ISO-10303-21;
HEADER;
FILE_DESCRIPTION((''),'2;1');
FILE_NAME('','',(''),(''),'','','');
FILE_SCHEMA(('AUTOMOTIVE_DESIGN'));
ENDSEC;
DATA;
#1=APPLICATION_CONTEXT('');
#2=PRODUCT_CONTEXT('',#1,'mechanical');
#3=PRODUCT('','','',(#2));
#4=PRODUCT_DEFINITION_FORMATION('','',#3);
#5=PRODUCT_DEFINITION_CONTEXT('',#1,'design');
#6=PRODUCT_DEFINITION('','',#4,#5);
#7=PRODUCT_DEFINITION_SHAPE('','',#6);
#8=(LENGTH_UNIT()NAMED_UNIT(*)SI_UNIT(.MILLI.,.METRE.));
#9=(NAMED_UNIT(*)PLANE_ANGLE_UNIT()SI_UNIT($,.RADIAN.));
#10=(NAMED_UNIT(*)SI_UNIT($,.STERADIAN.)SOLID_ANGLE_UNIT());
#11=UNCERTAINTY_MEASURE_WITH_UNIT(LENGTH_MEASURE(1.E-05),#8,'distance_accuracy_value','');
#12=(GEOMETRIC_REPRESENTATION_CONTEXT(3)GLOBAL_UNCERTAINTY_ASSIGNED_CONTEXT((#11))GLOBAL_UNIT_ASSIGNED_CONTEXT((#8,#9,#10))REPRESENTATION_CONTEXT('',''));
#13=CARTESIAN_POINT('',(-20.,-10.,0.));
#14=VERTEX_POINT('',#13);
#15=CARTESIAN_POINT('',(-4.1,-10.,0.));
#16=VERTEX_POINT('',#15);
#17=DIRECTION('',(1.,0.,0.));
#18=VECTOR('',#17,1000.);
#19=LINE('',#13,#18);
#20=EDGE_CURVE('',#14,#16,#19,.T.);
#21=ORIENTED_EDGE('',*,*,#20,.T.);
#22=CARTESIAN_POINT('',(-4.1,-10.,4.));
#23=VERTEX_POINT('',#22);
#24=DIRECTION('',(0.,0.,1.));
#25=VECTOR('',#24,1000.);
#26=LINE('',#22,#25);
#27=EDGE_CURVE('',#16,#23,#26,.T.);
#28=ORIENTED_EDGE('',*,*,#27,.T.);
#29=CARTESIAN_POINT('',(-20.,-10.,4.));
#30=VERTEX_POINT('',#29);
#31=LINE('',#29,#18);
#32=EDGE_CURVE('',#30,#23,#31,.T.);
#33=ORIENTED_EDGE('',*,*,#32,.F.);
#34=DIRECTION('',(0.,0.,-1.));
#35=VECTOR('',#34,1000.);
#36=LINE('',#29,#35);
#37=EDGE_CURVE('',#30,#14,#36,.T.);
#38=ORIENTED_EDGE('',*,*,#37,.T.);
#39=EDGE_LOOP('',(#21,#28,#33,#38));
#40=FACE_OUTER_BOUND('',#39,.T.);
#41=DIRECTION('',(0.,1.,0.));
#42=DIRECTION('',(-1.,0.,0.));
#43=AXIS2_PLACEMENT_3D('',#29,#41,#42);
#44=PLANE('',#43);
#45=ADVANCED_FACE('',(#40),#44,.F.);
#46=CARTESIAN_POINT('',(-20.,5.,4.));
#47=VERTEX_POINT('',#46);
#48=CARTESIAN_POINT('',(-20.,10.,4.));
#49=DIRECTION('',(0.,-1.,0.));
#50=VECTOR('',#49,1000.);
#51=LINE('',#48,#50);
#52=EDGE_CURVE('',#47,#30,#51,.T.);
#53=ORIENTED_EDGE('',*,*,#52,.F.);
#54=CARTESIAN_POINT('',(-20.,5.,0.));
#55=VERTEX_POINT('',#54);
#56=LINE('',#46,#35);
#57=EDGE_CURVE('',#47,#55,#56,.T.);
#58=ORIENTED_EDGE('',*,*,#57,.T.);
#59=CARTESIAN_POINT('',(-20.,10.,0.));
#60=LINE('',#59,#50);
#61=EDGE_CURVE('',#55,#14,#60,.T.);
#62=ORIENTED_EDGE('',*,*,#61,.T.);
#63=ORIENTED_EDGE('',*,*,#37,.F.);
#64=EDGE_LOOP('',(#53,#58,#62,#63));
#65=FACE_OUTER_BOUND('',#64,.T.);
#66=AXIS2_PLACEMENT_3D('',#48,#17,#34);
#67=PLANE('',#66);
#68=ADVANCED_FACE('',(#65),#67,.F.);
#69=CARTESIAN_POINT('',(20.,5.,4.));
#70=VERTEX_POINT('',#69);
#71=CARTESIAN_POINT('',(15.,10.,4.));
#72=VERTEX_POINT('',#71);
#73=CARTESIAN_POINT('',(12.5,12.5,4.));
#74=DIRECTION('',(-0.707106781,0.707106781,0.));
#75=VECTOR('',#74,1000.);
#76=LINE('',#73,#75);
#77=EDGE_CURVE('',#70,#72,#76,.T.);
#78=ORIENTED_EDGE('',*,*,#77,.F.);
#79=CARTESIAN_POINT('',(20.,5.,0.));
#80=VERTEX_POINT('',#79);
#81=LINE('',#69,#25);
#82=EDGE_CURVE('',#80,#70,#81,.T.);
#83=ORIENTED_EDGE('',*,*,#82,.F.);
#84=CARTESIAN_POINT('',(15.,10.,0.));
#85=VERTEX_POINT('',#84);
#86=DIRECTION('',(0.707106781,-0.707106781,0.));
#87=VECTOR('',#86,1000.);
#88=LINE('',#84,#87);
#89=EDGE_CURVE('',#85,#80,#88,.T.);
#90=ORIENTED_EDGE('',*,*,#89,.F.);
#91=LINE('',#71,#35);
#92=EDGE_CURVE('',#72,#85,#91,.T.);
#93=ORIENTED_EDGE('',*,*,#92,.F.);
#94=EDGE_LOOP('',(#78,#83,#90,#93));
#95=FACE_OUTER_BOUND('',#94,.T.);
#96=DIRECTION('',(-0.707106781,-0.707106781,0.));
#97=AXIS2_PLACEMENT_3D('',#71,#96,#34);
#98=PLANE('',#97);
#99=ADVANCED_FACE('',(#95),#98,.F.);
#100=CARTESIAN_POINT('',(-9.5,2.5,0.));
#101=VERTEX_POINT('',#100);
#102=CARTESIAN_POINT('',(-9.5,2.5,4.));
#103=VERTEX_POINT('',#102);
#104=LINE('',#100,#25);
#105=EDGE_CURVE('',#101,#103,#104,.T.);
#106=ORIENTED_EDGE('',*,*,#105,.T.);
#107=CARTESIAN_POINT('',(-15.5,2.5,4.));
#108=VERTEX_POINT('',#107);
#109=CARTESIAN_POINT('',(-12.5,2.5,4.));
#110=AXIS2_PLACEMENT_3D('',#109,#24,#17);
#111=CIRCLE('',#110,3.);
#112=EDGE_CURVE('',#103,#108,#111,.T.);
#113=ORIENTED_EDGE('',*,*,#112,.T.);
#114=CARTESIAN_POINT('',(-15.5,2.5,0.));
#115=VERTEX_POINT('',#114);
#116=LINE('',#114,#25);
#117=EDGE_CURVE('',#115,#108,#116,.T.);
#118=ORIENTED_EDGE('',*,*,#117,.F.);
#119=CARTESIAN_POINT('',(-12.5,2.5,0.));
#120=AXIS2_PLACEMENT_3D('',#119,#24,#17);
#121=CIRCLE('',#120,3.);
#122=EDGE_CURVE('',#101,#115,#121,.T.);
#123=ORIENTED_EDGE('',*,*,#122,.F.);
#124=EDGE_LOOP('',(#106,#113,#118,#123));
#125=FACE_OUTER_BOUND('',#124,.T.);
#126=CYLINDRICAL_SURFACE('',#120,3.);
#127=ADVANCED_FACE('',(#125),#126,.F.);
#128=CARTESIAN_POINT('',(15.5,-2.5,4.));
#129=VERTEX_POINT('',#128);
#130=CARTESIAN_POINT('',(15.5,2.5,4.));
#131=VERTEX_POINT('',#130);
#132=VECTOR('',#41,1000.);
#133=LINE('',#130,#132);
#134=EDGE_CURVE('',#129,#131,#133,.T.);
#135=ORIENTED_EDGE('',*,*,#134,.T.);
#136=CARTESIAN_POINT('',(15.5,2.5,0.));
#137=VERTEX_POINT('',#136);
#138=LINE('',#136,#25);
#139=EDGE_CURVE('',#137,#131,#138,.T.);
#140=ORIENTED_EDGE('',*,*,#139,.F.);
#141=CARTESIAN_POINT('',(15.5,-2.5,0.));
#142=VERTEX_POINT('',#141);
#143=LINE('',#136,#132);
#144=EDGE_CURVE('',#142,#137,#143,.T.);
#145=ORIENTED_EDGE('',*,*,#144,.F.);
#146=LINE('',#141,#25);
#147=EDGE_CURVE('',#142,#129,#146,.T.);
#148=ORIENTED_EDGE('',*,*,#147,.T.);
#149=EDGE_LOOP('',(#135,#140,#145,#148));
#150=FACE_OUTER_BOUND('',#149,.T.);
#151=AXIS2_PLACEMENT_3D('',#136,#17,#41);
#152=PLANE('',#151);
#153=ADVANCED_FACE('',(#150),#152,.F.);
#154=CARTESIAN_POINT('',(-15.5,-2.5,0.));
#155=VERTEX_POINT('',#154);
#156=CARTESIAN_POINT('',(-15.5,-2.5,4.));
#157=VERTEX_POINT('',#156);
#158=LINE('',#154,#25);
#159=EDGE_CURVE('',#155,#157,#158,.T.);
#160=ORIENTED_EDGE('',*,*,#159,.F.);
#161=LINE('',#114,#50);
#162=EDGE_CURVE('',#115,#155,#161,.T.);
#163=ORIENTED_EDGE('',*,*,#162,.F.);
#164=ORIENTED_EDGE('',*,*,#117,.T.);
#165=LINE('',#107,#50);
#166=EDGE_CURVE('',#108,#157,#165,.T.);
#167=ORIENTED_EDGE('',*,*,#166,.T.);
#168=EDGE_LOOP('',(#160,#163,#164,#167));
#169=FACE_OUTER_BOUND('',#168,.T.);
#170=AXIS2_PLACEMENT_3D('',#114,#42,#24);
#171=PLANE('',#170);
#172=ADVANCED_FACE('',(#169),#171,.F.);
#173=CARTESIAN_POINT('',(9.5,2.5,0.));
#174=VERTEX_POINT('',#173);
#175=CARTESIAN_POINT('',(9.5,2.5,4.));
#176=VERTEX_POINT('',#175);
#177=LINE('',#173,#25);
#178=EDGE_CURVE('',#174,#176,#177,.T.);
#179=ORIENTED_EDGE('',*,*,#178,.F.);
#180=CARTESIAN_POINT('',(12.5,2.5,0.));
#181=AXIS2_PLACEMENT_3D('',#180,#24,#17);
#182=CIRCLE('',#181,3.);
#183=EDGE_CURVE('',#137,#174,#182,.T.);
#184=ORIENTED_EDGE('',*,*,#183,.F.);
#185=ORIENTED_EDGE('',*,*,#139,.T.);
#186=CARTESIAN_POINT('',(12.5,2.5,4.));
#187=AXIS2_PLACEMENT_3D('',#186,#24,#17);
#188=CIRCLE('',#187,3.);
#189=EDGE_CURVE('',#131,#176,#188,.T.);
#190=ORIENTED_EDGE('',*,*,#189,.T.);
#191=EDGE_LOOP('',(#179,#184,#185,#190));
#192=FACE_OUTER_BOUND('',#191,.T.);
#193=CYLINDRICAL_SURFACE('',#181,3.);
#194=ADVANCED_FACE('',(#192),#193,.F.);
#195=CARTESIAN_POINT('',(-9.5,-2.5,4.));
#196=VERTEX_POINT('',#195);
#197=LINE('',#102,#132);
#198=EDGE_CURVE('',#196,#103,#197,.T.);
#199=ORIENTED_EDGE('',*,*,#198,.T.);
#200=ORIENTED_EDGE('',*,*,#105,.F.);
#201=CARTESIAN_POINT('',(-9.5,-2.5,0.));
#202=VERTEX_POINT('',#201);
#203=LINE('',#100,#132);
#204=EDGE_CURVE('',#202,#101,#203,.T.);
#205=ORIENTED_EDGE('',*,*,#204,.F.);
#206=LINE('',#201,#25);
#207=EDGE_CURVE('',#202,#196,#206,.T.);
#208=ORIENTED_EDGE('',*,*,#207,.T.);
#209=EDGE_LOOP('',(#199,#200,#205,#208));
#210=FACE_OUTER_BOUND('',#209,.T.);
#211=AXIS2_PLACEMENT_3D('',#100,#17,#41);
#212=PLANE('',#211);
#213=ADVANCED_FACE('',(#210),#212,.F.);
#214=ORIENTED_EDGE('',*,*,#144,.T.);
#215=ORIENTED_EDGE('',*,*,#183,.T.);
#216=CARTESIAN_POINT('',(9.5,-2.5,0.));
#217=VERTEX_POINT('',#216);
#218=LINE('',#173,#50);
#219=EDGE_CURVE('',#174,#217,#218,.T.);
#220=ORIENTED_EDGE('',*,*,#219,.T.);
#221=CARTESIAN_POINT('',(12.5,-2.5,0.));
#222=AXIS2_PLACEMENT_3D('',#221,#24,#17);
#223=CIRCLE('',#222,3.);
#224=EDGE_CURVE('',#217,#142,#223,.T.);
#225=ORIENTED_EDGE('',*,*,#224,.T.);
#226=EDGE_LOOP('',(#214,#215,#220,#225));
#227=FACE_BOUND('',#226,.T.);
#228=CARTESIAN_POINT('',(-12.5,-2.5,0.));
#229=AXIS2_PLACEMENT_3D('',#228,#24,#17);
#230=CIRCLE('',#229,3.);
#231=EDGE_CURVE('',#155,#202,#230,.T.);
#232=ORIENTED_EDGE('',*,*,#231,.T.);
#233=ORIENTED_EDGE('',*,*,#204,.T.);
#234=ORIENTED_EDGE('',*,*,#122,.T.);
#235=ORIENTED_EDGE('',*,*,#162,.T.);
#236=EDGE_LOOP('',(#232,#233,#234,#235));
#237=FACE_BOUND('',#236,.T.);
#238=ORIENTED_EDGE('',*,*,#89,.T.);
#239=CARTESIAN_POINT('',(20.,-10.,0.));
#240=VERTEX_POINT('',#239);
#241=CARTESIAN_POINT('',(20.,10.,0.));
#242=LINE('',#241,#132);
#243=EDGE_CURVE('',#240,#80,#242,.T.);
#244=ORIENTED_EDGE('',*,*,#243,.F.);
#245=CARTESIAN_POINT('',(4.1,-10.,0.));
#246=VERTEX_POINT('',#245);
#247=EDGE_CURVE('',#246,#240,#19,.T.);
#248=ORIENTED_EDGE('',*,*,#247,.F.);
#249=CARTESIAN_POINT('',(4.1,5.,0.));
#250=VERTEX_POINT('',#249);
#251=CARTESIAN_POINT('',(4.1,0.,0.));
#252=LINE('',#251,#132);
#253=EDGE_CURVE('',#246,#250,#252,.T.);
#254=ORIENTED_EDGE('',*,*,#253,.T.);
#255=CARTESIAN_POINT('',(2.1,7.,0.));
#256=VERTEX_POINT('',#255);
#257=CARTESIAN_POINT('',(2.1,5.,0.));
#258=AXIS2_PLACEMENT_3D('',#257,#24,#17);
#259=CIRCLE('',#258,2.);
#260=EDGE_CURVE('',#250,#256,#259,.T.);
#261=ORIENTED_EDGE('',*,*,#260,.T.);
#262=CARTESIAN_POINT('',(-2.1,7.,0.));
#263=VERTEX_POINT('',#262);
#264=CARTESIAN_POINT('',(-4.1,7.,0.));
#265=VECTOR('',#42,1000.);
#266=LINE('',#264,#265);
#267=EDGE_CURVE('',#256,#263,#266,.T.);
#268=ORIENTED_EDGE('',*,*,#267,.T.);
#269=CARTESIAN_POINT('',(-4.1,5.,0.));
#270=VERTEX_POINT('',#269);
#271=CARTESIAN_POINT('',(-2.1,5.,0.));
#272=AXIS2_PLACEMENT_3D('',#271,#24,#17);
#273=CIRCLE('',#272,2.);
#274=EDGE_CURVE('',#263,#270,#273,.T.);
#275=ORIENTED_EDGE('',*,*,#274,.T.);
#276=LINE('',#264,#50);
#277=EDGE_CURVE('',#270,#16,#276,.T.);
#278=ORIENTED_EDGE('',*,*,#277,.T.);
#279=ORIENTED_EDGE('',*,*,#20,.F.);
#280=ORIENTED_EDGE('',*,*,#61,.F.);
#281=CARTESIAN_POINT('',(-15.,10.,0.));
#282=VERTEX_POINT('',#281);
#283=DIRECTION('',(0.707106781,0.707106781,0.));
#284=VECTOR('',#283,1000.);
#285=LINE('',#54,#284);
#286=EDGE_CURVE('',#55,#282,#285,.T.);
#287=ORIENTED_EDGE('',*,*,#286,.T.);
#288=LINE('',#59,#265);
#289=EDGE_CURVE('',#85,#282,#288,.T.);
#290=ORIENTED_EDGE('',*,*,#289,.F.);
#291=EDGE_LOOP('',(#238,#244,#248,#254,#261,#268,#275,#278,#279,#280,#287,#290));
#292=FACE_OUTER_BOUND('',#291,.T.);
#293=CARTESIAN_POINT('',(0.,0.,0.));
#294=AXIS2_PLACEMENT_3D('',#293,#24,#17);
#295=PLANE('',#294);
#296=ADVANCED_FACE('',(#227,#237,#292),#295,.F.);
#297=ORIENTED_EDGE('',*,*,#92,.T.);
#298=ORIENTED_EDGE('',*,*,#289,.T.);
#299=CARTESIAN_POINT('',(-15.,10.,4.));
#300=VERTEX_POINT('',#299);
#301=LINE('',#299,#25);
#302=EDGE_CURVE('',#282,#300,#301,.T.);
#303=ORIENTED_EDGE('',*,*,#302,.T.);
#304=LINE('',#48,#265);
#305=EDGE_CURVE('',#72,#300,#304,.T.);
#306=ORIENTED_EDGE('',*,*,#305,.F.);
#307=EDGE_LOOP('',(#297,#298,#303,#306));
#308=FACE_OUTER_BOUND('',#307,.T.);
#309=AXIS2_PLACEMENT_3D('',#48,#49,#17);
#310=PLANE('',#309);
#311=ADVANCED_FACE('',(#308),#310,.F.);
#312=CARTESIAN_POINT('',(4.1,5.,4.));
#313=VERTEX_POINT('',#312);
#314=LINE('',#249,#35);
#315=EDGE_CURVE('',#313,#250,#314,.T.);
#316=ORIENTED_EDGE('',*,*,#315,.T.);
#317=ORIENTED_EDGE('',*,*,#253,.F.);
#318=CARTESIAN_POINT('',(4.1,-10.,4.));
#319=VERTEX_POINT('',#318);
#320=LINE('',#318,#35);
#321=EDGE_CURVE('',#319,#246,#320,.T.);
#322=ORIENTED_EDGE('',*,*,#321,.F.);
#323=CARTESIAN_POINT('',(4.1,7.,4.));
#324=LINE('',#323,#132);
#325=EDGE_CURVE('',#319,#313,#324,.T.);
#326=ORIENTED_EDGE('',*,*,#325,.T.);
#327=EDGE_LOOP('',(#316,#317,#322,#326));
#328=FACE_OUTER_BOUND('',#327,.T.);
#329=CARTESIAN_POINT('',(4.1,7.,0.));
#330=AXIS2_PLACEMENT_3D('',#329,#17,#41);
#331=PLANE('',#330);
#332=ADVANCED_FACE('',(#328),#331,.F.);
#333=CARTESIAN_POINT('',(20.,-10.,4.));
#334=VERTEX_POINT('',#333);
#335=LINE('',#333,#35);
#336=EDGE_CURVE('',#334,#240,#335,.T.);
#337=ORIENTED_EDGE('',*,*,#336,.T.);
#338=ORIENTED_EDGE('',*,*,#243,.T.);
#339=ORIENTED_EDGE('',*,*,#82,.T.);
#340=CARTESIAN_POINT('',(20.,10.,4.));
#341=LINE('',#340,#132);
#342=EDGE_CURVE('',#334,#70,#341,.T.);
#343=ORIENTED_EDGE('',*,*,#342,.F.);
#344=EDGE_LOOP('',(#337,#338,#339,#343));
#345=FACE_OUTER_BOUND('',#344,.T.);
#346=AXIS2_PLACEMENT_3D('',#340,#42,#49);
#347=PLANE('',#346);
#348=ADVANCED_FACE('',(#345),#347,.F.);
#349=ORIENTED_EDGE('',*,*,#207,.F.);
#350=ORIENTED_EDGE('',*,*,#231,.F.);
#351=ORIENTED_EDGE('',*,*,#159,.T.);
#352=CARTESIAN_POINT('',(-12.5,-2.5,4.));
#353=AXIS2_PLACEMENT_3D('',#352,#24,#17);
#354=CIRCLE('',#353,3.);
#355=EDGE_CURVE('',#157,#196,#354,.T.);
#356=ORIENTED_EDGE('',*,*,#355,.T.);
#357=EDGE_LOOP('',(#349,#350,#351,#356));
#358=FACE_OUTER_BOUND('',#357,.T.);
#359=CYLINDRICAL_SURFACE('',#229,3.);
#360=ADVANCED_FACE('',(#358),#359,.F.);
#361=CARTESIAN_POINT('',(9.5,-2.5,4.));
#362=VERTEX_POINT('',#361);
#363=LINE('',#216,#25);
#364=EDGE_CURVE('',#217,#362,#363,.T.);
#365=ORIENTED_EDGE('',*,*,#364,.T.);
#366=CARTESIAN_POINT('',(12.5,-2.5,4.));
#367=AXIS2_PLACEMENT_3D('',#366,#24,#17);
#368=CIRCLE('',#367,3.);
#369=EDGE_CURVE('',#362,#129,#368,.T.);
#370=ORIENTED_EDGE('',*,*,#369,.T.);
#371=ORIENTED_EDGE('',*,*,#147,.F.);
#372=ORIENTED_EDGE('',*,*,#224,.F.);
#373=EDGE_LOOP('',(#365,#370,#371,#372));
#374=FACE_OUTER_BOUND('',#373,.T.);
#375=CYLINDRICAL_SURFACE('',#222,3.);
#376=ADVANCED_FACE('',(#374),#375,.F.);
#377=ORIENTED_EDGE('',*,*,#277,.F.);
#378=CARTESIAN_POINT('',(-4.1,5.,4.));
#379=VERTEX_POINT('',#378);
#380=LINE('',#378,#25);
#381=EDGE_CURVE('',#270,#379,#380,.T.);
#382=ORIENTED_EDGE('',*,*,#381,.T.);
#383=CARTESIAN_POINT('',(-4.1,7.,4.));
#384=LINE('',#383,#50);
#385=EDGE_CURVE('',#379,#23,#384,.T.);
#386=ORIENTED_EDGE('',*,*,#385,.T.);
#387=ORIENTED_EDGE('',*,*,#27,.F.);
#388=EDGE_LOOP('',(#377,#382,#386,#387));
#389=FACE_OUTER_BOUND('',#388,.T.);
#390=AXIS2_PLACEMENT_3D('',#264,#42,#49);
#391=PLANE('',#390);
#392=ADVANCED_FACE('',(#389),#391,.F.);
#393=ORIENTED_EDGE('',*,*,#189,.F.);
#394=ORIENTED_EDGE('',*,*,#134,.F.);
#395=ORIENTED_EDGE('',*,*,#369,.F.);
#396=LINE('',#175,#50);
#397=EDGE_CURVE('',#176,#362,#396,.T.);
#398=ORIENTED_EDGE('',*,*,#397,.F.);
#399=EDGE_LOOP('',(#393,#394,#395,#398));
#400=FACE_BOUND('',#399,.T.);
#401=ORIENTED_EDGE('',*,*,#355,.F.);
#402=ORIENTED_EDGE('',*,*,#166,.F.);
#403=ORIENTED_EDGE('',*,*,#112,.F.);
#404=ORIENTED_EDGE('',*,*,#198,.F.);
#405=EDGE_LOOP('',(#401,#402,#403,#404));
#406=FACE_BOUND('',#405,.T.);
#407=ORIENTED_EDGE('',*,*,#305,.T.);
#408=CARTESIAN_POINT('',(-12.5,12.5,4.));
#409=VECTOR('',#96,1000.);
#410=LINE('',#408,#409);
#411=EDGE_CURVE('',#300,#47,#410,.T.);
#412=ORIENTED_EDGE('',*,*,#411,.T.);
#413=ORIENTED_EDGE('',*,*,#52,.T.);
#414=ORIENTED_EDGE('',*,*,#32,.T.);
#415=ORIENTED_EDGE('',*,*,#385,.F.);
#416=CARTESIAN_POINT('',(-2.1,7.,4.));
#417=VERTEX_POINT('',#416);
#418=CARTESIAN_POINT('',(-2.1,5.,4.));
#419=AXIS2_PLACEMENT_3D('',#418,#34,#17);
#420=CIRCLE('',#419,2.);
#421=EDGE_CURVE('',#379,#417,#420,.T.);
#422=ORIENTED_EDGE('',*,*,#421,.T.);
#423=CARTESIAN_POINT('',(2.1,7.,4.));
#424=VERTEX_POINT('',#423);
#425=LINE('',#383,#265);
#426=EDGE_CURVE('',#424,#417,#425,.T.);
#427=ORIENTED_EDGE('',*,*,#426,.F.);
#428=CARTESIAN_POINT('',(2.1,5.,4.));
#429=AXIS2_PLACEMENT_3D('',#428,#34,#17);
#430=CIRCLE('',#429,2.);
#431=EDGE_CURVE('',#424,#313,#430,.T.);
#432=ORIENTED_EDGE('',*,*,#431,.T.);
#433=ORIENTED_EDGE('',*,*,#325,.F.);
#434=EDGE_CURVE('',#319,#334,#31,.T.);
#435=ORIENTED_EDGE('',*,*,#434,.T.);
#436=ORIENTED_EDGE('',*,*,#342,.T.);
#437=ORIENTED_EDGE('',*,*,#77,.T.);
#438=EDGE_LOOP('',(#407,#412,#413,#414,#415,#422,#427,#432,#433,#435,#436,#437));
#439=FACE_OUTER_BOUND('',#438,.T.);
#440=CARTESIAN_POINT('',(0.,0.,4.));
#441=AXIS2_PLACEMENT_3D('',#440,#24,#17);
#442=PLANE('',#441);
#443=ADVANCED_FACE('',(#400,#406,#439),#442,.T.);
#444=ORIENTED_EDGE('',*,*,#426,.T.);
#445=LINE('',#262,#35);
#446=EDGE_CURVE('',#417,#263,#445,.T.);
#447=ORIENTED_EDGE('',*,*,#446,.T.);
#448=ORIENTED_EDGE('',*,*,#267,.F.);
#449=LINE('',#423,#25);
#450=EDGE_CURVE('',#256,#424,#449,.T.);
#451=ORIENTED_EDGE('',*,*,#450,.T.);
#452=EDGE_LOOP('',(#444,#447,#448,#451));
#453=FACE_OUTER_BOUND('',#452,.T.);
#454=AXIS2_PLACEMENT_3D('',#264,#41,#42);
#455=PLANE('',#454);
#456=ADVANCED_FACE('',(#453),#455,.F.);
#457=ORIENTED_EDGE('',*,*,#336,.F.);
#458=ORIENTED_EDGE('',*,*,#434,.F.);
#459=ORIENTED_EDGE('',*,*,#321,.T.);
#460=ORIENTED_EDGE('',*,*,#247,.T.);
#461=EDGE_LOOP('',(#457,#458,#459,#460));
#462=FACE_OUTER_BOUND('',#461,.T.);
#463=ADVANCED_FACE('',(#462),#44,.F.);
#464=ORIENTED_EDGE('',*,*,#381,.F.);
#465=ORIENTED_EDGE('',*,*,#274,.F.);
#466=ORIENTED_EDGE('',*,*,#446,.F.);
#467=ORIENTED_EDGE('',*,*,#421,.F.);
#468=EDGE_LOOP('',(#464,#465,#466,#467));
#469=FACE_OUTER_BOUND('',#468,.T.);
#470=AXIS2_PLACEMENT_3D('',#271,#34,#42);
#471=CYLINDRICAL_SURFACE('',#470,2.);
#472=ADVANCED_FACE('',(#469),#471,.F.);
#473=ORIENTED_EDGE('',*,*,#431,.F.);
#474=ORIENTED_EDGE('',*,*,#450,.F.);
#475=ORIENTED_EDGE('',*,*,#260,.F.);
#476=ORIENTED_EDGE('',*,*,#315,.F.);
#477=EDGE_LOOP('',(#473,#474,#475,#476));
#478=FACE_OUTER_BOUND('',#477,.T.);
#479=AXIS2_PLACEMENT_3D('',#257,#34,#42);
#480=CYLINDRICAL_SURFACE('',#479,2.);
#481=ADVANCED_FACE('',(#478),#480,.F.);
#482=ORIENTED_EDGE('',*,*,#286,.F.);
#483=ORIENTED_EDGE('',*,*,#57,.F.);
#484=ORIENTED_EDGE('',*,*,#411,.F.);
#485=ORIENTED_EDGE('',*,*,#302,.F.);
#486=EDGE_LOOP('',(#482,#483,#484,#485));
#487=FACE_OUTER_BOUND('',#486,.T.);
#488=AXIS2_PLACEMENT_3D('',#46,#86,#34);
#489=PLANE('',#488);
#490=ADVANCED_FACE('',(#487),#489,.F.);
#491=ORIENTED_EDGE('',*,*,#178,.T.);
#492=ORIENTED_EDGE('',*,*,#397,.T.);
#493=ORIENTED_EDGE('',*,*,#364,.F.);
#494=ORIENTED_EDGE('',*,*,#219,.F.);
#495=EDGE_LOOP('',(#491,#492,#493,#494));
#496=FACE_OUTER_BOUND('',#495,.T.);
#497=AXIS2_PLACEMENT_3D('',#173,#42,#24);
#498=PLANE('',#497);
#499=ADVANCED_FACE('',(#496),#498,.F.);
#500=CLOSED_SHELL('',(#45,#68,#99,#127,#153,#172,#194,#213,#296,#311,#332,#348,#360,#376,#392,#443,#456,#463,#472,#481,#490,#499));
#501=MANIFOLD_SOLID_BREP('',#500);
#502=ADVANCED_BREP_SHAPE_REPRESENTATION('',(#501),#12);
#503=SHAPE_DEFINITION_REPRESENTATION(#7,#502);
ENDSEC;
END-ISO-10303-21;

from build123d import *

# Parameters (mm, degrees)
SKETCH_1_W             = 40
SKETCH_1_H             = 20
EXTRUDE_1_DEPTH        = 4
CUT_EXTRUDE_1_DEPTH    = 23.715633383
CHAMFER_1_SIZE         = 5
SKETCH_3_R             = 3
CUT_EXTRUDE_2_DEPTH    = 23.715633383
CUT_EXTRUDE_3_DEPTH    = 23.715633383
PATTERN_LINEAR_1_COUNT = 2
PATTERN_LINEAR_1_PITCH = 25
FILLET_1_R             = 2


with BuildPart() as part:
    # 草图1 → 凸台-拉伸1 (new body)
    with BuildSketch(Plane.XY):
        Rectangle(SKETCH_1_W, SKETCH_1_H)
    extrude(amount=EXTRUDE_1_DEPTH)

    # 草图2 → 切除-拉伸1 (cut, through all)
    with BuildSketch(Plane.XY.offset(4)):
        with BuildLine():
            Line((4.1, 7), (4.1, -18.947287746))
            ThreePointArc((4.1, -18.947287746), (0, -23.047287746), (-4.1, -18.947287746))
            Line((-4.1, -18.947287746), (-4.1, 7))
            Line((-4.1, 7), (4.1, 7))
        make_face()
    extrude(amount=-CUT_EXTRUDE_1_DEPTH, mode=Mode.SUBTRACT)

    # 倒角1
    chamfer_1_edges = [part.edges().sort_by_distance(p)[0] for p in [
        (-20, 10, 2),
        (20, 10, 2),
    ]]
    chamfer(chamfer_1_edges, length=CHAMFER_1_SIZE)

    # 草图3 → 切除-拉伸2 (cut, through all)
    with BuildSketch(Plane.XY.offset(4)):
        with Locations((-12.5, 0)):
            Circle(SKETCH_3_R)
        with Locations((12.5, 0)):
            Circle(SKETCH_3_R)
    extrude(amount=-CUT_EXTRUDE_2_DEPTH, mode=Mode.SUBTRACT)

    # 草图5 → 切除-拉伸3 (cut, through all)
    with BuildSketch(Plane.XY.offset(4)):
        with BuildLine():
            Line((-9.5, 2.5), (-9.5, -2.5))
            ThreePointArc((-9.5, -2.5), (-12.5, -5.5), (-15.5, -2.5))
            Line((-15.5, -2.5), (-15.5, 2.5))
            ThreePointArc((-15.5, 2.5), (-12.5, 5.5), (-9.5, 2.5))
        make_face()
    cut_extrude_3 = extrude(amount=-CUT_EXTRUDE_3_DEPTH, mode=Mode.SUBTRACT)

    # 阵列(线性)1: 切除-拉伸3 ×2
    with Locations(*[(i * PATTERN_LINEAR_1_PITCH, 0, 0) for i in range(1, PATTERN_LINEAR_1_COUNT)]):
        add(cut_extrude_3, mode=Mode.SUBTRACT)

    # 圆角1
    fillet_1_edges = [part.edges().sort_by_distance(p)[0] for p in [
        (4.1, 7, 2),
        (-4.1, 7, 2),
    ]]
    fillet(fillet_1_edges, radius=FILLET_1_R)


solid = part.part
